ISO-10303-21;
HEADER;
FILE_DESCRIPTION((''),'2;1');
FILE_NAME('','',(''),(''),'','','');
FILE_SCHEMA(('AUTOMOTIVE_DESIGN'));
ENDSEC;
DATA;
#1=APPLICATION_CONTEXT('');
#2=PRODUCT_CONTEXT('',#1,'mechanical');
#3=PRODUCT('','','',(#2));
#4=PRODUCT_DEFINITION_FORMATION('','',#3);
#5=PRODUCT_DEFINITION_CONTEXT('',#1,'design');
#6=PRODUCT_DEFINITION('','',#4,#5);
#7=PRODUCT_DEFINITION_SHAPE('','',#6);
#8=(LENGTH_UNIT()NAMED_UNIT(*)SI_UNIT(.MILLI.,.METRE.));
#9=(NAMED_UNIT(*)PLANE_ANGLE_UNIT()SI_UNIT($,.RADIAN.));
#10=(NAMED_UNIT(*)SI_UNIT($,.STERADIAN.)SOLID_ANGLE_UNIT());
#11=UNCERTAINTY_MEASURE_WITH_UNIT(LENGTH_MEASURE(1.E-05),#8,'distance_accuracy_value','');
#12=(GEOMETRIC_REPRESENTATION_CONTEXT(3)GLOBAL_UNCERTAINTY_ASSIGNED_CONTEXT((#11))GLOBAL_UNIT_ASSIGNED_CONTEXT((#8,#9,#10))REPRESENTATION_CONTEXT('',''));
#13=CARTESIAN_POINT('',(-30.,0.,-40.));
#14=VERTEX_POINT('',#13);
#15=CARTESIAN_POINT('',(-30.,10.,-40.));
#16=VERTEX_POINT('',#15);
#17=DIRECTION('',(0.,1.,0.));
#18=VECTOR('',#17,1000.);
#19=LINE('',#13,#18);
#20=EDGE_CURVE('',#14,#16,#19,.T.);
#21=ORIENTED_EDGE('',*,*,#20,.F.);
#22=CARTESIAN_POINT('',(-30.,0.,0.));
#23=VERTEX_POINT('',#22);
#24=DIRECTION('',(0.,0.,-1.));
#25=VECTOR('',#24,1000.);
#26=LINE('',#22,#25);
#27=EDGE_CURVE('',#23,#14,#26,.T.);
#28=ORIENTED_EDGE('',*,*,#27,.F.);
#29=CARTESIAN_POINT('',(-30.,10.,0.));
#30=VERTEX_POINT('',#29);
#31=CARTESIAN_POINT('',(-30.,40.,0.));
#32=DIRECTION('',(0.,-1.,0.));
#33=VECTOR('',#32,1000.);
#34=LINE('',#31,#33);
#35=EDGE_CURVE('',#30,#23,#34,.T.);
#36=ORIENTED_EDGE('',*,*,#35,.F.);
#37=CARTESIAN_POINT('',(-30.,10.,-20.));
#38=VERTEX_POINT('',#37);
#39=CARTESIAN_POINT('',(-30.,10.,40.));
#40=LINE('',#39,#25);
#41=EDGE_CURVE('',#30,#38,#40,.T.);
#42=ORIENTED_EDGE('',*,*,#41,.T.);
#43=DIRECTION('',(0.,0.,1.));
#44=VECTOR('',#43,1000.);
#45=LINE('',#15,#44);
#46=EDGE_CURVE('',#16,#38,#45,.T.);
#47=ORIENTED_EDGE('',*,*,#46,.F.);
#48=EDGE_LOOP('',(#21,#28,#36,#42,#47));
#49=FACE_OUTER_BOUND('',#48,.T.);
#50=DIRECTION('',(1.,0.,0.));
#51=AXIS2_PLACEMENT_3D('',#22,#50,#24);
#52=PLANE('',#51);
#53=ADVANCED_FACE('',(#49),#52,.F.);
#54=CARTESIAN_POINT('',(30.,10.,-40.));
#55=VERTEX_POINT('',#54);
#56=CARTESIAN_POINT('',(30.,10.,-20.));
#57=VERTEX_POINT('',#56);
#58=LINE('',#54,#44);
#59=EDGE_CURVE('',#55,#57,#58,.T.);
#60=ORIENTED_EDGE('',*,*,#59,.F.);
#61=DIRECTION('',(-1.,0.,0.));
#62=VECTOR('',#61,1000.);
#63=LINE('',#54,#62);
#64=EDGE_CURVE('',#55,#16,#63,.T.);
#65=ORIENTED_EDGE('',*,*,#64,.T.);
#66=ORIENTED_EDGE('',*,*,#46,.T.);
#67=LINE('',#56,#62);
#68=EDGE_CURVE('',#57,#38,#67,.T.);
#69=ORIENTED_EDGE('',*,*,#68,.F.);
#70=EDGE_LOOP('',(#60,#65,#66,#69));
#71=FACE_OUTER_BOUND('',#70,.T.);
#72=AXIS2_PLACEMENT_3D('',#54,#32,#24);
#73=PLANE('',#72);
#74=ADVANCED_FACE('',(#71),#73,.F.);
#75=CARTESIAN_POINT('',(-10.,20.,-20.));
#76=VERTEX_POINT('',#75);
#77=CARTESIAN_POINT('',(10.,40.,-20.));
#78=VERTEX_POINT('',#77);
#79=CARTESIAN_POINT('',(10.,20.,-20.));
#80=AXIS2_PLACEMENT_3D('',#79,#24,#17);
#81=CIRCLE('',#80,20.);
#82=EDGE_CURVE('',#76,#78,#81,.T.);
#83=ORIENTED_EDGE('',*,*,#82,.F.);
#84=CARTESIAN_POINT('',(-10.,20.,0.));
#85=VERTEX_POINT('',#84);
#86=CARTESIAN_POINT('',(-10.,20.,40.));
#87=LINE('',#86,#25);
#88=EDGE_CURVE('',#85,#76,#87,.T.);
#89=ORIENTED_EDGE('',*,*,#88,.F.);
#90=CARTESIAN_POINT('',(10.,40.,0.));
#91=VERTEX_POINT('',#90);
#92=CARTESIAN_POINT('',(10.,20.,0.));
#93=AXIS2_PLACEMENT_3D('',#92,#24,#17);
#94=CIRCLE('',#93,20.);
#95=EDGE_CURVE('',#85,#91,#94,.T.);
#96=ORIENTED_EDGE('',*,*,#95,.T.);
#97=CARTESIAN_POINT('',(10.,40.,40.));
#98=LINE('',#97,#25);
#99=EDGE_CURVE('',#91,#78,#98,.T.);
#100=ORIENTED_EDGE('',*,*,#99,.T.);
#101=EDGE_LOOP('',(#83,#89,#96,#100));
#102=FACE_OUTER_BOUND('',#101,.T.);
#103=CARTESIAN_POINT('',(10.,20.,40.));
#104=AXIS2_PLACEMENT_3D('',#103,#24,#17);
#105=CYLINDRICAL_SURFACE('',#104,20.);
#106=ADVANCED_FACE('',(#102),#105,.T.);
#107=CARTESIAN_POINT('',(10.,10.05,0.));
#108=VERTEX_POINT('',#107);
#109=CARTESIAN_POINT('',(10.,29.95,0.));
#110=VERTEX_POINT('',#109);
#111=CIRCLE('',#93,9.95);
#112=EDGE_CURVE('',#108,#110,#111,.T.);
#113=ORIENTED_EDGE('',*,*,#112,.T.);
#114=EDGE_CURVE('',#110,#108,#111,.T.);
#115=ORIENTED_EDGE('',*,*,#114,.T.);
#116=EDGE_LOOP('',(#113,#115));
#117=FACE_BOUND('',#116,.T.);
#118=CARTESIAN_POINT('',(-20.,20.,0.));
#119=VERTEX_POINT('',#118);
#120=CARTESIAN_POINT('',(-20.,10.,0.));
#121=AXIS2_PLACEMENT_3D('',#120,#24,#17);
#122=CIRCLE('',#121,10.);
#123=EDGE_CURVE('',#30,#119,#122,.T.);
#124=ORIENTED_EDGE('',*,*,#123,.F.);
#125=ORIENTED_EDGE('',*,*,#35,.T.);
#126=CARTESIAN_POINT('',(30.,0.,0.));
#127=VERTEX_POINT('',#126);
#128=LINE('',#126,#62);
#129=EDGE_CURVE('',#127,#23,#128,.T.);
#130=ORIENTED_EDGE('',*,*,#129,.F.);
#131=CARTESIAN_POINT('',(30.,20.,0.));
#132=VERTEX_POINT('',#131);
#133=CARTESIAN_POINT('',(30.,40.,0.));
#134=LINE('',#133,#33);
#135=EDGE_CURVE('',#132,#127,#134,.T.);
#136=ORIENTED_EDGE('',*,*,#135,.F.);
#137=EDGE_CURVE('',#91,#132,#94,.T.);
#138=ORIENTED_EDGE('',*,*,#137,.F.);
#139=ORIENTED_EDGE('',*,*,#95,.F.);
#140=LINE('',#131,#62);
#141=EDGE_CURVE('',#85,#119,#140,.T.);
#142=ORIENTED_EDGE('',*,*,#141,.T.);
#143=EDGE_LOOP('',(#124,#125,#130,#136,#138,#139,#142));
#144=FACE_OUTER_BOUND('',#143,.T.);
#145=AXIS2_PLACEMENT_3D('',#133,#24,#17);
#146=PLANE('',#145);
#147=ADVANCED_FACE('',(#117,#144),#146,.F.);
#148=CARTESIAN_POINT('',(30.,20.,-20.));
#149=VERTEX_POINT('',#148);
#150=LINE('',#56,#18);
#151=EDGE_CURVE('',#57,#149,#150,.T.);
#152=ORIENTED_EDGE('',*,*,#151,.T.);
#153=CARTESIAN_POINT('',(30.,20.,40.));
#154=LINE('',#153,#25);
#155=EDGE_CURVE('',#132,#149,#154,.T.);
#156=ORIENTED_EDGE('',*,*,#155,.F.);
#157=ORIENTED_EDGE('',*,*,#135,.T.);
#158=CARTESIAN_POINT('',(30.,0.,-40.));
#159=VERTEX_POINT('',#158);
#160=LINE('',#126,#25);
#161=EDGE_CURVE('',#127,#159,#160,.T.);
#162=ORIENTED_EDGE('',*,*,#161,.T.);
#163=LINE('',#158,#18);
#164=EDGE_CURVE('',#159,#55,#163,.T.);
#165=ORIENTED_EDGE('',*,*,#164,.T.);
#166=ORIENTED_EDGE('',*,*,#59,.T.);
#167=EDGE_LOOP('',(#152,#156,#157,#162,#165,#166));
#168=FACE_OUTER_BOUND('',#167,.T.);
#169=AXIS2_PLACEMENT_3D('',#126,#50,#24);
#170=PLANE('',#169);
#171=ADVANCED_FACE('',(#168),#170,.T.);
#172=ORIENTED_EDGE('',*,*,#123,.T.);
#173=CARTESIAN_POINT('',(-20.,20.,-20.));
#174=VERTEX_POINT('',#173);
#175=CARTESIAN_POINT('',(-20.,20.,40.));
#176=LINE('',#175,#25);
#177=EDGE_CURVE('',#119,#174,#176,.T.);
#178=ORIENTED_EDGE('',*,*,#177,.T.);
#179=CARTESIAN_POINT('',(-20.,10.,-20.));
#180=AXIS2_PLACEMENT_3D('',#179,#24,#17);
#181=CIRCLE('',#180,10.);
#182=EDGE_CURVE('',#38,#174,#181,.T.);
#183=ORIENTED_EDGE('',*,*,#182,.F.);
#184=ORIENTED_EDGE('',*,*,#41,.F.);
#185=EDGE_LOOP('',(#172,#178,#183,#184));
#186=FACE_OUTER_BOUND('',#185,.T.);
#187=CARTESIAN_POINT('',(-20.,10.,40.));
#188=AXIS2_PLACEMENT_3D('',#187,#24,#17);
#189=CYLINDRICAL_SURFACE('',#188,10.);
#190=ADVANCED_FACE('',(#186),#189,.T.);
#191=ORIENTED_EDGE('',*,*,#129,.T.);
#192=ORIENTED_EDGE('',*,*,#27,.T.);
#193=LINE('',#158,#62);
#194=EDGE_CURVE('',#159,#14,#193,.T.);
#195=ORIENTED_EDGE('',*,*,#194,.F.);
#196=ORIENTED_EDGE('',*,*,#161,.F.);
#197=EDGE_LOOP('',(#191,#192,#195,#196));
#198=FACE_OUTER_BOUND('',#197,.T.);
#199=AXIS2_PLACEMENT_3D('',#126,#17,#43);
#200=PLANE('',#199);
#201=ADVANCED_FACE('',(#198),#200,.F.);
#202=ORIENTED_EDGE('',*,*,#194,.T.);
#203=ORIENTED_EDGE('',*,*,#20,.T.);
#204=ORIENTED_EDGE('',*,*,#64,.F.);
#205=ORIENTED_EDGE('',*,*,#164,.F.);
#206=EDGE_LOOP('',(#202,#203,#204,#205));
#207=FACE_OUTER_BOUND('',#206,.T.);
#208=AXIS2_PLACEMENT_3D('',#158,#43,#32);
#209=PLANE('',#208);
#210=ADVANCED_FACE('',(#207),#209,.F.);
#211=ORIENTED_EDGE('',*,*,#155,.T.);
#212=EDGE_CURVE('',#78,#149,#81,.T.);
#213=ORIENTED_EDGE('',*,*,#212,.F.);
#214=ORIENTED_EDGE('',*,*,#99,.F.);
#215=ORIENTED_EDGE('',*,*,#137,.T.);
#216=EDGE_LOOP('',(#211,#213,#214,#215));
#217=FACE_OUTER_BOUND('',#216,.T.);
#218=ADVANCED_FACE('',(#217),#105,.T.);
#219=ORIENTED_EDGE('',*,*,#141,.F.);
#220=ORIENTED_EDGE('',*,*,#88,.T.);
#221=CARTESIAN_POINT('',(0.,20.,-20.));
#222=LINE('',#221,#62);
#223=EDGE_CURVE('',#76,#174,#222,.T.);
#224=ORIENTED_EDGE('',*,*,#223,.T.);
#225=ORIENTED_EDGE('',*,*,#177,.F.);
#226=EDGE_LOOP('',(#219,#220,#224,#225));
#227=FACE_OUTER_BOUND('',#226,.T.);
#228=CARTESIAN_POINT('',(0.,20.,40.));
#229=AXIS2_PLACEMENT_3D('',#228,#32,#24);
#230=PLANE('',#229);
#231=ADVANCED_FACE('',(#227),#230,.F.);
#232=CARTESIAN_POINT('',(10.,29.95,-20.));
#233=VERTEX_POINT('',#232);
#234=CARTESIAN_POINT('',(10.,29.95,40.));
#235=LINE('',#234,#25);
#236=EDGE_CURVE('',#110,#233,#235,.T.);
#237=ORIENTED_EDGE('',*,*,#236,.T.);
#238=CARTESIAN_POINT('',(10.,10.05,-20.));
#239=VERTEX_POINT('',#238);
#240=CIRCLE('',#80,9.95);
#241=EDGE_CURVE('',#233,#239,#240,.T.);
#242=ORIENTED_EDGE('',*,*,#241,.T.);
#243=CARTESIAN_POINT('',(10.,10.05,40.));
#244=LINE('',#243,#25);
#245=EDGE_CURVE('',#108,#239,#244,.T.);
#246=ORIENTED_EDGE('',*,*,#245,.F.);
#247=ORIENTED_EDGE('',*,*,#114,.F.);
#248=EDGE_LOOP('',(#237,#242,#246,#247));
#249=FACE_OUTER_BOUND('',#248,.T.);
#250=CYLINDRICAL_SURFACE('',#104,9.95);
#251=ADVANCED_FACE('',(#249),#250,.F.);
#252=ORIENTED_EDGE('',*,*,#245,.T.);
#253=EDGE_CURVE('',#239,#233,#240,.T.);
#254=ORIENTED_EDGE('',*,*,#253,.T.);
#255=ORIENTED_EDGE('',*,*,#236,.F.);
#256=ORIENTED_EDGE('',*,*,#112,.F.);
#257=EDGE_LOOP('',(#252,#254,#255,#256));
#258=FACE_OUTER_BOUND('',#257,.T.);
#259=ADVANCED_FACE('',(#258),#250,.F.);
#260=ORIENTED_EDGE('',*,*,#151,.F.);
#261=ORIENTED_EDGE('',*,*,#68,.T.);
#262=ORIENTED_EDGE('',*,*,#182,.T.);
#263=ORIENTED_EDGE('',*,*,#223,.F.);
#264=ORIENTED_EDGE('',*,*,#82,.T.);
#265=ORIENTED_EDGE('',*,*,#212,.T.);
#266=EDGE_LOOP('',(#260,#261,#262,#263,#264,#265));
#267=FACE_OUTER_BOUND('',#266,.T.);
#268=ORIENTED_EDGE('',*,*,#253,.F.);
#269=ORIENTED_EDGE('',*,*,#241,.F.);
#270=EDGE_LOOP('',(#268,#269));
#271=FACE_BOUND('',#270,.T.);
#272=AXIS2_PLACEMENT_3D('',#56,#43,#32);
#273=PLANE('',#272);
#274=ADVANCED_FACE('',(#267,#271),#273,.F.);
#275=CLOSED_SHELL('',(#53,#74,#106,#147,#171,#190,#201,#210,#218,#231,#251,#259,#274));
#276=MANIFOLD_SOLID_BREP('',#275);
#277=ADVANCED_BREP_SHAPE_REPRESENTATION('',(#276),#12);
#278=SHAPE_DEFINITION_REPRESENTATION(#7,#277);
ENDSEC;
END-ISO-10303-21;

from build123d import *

# Parameters (mm, degrees)
BRACKET_BODY_DEPTH      = 30
BOSS_ROUNDING_SKETCH_R  = 9.95
BOSS_ROUNDING_CUT_DEPTH = 60
BORE_CUT_DEPTH          = 60


with BuildPart() as part:
    # Bracket Profile Sketch → Bracket Body (new, symmetric)
    with BuildSketch(Plane(origin=(0, 0, 0), x_dir=(0, 0, -1), z_dir=(1, 0, 0))):
        Polygon((0, 0), (40, 0), (40, 10), (20, 10), (20, 40), (0, 40), align=None)
    extrude(amount=BRACKET_BODY_DEPTH, both=True)

    # Boss Rounding Sketch → Boss Rounding Cut (cut)
    with BuildSketch(Plane(origin=(0, 0, -20), x_dir=(-1, 0, 0), z_dir=(0, 0, -1))):
        with Locations(Location((-10, 20, 0), (0, 0, 90))):
            Circle(BOSS_ROUNDING_SKETCH_R)
    extrude(amount=-BOSS_ROUNDING_CUT_DEPTH, mode=Mode.SUBTRACT)

    # Bore Sketch → Bore Cut (cut)
    with BuildSketch(Plane(origin=(0, 0, -20), x_dir=(-1, 0, 0), z_dir=(0, 0, -1))):
        with BuildLine():
            ThreePointArc((-30, 20), (-24.142135624, 34.142135624), (-10, 40))
            Line((-10, 40), (-30, 40))
            Line((-30, 40), (-30, 20))
        make_face()
        with BuildLine():
            ThreePointArc((-10, 40), (4.142135624, 34.142135624), (10, 20))
            Line((10, 20), (20, 20))
            ThreePointArc((20, 20), (27.071067812, 17.071067812), (30, 10))
            Line((30, 10), (30, 40))
            Line((30, 40), (-10, 40))
        make_face()
    extrude(amount=-BORE_CUT_DEPTH, mode=Mode.SUBTRACT)


solid = part.part
